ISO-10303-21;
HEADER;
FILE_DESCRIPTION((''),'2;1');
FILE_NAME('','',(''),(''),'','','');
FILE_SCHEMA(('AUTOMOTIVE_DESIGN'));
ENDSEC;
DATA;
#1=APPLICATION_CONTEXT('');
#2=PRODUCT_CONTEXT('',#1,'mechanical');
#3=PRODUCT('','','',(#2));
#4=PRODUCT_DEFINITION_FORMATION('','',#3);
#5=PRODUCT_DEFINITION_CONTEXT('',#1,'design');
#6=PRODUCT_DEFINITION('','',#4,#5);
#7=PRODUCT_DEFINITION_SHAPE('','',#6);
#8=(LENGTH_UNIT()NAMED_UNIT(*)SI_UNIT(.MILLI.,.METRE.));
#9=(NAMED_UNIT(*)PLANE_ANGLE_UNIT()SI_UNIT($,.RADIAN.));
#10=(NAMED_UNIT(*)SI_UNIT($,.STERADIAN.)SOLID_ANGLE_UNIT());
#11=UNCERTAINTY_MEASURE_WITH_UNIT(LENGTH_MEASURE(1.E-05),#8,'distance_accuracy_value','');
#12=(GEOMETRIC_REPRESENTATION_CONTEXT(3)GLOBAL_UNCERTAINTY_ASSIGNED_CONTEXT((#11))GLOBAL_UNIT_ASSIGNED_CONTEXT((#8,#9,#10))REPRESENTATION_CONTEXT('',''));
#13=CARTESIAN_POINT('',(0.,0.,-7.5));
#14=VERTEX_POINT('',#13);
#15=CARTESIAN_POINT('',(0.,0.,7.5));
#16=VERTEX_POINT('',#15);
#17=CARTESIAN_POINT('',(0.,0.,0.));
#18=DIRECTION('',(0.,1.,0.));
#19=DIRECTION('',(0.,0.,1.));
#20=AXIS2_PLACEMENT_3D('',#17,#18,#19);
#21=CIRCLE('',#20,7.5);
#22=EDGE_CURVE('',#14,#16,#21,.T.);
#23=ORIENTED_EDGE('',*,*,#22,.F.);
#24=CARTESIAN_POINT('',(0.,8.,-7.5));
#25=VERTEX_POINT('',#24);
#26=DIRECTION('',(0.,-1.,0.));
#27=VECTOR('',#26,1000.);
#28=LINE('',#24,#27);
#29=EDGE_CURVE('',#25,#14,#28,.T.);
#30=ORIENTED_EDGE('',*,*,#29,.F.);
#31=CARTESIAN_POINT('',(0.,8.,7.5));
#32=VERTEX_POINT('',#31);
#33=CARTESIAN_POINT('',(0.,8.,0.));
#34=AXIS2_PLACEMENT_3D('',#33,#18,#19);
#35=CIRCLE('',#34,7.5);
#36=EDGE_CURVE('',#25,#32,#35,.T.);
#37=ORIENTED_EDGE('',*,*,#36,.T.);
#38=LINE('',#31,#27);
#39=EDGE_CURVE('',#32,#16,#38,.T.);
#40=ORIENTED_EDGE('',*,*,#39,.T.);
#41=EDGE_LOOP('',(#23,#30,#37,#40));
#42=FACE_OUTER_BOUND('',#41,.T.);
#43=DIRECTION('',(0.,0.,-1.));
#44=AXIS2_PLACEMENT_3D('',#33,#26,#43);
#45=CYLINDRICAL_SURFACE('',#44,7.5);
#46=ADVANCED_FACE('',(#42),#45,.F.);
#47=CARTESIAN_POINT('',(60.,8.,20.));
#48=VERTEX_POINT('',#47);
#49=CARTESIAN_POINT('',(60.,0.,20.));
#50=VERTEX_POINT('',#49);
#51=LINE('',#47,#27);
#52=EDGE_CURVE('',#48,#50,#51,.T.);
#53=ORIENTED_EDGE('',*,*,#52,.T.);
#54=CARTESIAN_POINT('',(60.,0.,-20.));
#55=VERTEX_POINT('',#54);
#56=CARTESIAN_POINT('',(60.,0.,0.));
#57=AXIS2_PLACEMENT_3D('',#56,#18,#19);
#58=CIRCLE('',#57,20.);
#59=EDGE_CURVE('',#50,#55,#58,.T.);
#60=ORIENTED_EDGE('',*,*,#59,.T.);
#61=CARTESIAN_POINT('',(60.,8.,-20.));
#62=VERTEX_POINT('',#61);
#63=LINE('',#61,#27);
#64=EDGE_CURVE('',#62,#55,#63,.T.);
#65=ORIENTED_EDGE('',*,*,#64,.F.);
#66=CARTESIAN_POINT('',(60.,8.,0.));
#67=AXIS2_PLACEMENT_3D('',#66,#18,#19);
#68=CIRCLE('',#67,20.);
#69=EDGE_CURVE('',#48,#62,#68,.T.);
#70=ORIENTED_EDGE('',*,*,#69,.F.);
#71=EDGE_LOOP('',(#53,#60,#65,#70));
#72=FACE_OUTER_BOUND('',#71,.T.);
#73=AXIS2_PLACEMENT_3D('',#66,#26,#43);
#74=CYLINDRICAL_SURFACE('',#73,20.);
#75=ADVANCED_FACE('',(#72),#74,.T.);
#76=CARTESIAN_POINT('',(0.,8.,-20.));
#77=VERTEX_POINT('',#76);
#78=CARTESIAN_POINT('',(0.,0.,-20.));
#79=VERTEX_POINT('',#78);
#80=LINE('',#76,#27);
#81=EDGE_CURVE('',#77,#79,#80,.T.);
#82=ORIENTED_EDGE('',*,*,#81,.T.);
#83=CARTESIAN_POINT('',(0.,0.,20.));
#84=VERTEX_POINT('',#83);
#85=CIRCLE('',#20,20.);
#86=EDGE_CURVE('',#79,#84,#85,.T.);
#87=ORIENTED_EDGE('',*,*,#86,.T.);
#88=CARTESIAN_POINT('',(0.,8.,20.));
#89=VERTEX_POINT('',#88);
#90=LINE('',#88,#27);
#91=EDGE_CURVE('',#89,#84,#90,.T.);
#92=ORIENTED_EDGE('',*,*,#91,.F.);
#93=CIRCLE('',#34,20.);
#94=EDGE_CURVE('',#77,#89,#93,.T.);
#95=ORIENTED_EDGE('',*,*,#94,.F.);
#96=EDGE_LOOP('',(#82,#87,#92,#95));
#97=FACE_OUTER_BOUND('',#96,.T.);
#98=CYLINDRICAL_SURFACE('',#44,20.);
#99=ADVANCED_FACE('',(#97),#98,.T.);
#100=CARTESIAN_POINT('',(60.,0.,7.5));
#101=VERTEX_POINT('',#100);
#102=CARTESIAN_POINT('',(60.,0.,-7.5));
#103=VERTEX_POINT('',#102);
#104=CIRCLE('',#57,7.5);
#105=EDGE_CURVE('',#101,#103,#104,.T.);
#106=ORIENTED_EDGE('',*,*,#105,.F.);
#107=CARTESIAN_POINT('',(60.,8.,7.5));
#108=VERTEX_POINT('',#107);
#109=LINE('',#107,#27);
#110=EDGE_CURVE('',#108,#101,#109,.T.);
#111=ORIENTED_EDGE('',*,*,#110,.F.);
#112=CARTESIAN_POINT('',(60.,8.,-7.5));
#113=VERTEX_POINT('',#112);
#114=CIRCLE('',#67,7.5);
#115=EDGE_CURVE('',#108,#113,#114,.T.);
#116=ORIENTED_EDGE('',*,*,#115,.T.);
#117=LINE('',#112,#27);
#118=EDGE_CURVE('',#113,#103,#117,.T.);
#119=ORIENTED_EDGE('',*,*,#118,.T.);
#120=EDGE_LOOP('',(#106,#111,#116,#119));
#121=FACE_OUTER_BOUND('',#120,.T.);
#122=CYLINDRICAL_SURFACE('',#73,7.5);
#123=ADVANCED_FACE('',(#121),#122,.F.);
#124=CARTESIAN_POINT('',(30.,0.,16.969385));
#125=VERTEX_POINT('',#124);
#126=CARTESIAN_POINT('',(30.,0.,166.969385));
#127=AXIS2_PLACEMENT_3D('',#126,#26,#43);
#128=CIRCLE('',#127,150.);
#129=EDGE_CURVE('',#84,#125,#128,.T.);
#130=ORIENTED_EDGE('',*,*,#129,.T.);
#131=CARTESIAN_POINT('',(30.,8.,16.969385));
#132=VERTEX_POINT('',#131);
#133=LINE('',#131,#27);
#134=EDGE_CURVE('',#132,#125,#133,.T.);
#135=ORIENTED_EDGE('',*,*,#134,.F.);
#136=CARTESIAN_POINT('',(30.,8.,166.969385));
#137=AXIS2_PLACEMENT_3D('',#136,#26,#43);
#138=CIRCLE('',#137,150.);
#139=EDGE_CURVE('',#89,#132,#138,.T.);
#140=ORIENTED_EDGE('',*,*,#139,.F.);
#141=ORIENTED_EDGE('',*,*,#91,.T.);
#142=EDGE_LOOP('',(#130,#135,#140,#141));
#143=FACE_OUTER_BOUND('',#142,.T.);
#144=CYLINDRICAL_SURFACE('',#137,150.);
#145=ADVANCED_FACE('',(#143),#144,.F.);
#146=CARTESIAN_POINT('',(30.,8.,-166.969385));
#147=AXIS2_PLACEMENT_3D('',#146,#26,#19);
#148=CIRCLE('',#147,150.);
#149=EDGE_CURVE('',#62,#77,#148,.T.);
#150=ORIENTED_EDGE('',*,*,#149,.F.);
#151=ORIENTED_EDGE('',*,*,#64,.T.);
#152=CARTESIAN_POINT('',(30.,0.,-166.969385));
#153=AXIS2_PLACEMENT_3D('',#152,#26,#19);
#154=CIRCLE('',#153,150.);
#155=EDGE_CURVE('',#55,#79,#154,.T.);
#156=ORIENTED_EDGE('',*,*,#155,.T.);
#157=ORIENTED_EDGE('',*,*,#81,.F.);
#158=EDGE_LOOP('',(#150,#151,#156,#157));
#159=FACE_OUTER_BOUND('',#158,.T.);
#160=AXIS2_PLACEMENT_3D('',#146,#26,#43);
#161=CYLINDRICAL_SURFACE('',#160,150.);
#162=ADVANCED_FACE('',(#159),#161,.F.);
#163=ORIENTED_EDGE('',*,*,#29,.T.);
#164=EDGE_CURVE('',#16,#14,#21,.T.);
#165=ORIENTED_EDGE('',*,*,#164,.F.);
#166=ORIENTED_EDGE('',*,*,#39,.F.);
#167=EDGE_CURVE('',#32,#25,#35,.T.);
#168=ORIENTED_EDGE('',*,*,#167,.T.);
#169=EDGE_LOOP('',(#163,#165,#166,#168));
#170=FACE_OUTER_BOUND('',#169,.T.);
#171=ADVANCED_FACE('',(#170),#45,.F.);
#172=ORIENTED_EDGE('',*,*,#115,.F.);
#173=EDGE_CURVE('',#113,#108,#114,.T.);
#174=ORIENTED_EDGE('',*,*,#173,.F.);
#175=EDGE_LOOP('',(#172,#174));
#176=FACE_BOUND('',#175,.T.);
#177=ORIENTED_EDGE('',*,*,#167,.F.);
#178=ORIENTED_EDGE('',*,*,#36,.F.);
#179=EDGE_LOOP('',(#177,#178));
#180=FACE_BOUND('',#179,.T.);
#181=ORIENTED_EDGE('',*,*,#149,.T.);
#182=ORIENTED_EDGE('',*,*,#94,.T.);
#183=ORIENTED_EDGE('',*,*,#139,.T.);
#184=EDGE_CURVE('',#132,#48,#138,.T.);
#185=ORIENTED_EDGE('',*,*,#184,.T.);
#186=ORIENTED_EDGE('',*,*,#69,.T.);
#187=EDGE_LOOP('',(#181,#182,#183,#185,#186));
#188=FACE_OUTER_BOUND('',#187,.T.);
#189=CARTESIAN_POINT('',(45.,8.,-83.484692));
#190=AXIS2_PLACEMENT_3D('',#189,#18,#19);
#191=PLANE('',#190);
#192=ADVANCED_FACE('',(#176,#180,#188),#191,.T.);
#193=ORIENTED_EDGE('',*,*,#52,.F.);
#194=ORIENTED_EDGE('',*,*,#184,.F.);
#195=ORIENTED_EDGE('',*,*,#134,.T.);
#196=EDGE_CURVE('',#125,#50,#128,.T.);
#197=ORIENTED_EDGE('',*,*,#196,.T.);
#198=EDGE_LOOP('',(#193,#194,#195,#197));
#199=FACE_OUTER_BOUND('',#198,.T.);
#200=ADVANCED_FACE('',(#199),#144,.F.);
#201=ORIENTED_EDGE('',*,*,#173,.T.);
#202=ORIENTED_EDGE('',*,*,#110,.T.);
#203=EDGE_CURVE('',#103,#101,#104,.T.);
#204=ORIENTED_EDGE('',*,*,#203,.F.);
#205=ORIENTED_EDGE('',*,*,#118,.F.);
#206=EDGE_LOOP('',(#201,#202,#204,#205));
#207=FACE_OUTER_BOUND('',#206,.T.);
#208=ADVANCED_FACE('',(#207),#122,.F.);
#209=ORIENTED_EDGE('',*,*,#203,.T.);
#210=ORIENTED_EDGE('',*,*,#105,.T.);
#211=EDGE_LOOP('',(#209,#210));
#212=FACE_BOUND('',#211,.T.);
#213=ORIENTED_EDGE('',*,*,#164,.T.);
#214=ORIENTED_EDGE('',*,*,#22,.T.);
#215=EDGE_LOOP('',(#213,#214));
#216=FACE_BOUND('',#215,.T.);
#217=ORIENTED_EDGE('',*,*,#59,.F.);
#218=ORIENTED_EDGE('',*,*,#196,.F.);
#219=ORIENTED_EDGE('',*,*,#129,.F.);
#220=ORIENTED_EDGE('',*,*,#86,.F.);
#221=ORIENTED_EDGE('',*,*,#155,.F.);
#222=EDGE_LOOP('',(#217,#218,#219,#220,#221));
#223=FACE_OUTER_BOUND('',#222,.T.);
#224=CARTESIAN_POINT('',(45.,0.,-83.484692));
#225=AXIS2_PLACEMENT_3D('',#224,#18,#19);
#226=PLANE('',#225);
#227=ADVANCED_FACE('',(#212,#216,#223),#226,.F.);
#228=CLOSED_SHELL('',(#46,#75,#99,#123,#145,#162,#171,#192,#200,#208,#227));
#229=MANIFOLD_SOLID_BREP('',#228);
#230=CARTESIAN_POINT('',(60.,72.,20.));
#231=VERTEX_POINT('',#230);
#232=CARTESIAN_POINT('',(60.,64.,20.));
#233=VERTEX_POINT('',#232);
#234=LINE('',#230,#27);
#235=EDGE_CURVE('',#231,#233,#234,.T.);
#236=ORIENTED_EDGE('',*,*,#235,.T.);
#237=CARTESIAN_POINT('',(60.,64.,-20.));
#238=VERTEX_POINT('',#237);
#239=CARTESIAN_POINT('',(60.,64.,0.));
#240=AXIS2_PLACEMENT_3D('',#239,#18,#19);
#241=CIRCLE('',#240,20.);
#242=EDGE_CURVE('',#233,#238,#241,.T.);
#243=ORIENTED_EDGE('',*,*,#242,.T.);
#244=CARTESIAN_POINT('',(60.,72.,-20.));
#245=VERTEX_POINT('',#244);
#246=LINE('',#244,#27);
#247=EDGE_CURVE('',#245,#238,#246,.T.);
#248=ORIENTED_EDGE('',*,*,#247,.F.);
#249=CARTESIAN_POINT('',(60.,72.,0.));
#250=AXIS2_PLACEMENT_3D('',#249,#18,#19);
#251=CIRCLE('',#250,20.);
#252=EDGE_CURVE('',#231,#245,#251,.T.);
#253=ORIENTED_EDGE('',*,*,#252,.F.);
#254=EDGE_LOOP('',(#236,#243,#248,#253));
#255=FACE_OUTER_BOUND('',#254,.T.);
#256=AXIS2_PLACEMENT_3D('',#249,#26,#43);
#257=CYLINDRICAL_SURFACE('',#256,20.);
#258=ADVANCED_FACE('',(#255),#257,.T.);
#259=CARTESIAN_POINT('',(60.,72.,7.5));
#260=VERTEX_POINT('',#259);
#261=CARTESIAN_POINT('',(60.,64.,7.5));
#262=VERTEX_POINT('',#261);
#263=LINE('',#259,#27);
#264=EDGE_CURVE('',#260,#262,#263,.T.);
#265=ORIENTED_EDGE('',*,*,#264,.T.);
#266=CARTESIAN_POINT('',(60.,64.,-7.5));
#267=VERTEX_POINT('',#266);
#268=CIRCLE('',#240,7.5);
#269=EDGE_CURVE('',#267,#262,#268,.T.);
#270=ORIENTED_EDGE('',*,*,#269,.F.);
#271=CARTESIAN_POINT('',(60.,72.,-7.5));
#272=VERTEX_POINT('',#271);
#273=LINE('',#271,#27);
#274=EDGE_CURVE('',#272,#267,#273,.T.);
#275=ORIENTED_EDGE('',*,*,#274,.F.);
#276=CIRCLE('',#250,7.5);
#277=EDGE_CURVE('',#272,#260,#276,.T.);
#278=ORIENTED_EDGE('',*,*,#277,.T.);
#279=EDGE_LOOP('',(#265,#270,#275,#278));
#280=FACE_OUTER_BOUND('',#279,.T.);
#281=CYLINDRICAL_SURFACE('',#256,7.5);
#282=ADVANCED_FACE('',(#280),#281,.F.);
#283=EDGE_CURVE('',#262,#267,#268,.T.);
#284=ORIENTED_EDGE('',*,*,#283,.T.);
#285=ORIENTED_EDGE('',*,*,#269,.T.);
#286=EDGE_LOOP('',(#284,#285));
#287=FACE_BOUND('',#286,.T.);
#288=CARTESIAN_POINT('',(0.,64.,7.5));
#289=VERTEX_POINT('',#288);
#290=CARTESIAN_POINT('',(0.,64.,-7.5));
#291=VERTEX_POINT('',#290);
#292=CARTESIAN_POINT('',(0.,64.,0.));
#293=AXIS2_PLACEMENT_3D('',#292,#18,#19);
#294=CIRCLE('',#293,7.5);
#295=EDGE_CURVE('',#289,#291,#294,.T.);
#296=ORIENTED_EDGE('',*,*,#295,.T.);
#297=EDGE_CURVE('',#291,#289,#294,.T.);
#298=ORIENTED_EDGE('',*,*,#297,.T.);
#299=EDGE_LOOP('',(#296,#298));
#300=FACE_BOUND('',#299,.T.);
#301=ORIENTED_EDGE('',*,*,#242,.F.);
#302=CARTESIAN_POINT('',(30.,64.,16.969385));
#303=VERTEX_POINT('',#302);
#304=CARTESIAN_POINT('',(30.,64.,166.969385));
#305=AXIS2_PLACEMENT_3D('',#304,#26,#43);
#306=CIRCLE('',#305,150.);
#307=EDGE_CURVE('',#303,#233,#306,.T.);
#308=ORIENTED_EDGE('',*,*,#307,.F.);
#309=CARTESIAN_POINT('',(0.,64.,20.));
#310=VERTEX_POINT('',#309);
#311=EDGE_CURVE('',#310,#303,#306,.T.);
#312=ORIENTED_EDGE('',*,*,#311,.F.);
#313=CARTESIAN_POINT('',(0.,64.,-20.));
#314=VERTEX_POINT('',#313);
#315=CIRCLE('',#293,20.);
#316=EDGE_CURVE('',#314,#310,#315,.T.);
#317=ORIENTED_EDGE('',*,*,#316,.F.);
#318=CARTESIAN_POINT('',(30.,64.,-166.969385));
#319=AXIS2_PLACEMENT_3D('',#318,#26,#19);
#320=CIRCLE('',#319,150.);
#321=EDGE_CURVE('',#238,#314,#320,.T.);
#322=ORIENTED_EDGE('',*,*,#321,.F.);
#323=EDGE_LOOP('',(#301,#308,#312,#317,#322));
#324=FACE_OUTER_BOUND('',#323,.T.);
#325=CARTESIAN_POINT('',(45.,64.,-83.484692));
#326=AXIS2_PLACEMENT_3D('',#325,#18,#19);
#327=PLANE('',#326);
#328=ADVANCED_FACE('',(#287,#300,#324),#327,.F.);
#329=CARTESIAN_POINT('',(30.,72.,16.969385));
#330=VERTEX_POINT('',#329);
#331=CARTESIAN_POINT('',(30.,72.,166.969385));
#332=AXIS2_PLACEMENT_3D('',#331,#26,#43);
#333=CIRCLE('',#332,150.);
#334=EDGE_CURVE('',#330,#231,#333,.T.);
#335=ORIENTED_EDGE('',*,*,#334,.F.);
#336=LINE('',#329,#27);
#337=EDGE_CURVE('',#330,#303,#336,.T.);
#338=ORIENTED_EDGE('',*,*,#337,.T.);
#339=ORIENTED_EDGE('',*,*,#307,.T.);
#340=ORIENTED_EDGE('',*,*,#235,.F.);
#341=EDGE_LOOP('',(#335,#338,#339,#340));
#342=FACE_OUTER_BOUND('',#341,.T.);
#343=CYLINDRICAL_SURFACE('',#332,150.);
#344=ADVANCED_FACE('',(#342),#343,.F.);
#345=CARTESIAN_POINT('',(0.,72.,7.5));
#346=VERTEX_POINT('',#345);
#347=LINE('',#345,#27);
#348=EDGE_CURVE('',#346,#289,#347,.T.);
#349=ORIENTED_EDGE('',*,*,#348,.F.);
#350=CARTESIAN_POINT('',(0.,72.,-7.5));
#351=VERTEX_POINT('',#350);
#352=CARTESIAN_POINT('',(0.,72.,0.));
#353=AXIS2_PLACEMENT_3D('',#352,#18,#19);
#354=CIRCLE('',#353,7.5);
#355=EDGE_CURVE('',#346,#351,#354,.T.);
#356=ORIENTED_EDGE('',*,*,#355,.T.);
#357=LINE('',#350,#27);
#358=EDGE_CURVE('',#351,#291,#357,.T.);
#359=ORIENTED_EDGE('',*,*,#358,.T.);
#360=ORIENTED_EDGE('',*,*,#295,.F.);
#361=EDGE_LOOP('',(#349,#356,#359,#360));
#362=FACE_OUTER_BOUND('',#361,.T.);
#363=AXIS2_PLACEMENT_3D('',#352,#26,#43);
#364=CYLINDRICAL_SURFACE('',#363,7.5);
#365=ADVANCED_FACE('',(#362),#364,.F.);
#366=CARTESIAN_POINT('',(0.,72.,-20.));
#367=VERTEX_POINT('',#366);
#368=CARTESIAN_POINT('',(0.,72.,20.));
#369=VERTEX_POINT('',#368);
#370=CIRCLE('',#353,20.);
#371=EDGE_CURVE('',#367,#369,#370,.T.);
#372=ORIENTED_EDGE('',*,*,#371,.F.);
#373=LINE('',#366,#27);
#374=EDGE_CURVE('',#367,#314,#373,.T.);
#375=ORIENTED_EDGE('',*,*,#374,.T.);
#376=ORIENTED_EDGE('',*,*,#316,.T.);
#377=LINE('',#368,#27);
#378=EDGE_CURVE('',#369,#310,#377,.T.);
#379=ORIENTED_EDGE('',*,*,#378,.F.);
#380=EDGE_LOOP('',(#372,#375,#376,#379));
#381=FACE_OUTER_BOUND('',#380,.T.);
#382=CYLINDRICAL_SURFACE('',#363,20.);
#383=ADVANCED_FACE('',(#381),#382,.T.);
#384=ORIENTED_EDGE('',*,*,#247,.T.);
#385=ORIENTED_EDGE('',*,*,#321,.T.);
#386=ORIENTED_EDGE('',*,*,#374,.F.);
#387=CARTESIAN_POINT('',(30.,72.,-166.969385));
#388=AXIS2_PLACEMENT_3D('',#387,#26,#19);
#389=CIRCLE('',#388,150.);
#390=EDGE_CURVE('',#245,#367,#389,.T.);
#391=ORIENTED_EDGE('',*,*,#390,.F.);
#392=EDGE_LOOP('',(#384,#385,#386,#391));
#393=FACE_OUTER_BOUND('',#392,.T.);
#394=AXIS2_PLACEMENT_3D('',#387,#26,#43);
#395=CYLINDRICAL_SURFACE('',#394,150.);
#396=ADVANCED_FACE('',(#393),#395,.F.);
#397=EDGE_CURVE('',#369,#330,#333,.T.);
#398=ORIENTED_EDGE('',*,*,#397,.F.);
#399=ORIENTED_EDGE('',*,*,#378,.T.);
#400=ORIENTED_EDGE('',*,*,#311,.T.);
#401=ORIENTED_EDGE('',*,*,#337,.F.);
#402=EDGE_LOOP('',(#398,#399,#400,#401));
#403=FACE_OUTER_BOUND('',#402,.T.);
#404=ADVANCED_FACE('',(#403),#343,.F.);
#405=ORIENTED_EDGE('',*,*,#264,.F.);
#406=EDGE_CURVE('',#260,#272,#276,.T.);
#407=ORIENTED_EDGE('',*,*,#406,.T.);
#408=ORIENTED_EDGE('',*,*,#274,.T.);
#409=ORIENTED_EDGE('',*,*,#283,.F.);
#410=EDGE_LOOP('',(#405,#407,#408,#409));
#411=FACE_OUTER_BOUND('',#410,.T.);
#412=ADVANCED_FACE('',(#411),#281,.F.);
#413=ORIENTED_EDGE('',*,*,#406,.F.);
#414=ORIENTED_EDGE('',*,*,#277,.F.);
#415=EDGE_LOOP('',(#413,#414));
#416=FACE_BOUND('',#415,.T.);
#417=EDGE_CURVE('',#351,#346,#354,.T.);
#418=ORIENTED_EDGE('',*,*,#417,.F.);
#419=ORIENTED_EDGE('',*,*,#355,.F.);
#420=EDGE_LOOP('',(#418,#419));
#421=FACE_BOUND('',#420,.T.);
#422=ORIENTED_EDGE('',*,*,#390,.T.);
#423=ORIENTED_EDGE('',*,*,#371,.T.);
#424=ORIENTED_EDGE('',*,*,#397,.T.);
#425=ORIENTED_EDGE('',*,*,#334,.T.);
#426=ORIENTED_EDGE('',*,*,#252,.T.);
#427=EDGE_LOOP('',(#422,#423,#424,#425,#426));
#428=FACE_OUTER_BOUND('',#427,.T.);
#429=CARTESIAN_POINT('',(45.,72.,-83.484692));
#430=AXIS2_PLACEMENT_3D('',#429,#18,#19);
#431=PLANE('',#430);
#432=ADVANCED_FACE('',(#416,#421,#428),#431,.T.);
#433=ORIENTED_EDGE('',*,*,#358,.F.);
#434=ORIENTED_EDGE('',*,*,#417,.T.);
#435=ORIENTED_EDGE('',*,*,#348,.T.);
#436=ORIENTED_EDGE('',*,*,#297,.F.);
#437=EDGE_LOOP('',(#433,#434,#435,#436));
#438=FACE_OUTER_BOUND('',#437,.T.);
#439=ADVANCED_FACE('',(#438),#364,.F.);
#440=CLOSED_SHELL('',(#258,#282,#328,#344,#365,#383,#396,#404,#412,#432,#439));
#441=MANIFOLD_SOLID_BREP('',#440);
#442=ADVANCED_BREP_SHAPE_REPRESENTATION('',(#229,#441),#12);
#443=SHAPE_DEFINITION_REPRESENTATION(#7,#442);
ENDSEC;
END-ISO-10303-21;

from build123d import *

# Parameters (mm, degrees)
SKETCH1_R           = 7.5
BOSS_EXTRUDE1_DEPTH = 8
LPATTERN1_COUNT     = 2
LPATTERN1_PITCH     = 64


with BuildPart() as part:
    # Sketch1 → Boss-Extrude1 (new body)
    with BuildSketch(Plane(origin=(0, 0, 0), x_dir=(1, 0, 0), z_dir=(0, 1, 0))):
        with BuildLine():
            ThreePointArc((0, 20), (-20, 0), (0, -20))
            ThreePointArc((0, -20), (30, -16.969384567), (60, -20))
            ThreePointArc((60, -20), (80, 0), (60, 20))
            ThreePointArc((60, 20), (30, 16.969384567), (0, 20))
        make_face()
        with Locations(Location((0, 0, 0), (0, 0, 270))):
            Circle(SKETCH1_R, mode=Mode.SUBTRACT)
        with Locations(Location((60, 0, 0), (0, 0, 270))):
            Circle(SKETCH1_R, mode=Mode.SUBTRACT)
    extrude(amount=BOSS_EXTRUDE1_DEPTH)


with BuildPart() as lpattern1_1:
    # LPattern1: pattern copy
    add(part.part.moved(Location(Vector(0, 1, 0) * (1 * LPATTERN1_PITCH))))


solid = Compound([part.part, lpattern1_1.part])
